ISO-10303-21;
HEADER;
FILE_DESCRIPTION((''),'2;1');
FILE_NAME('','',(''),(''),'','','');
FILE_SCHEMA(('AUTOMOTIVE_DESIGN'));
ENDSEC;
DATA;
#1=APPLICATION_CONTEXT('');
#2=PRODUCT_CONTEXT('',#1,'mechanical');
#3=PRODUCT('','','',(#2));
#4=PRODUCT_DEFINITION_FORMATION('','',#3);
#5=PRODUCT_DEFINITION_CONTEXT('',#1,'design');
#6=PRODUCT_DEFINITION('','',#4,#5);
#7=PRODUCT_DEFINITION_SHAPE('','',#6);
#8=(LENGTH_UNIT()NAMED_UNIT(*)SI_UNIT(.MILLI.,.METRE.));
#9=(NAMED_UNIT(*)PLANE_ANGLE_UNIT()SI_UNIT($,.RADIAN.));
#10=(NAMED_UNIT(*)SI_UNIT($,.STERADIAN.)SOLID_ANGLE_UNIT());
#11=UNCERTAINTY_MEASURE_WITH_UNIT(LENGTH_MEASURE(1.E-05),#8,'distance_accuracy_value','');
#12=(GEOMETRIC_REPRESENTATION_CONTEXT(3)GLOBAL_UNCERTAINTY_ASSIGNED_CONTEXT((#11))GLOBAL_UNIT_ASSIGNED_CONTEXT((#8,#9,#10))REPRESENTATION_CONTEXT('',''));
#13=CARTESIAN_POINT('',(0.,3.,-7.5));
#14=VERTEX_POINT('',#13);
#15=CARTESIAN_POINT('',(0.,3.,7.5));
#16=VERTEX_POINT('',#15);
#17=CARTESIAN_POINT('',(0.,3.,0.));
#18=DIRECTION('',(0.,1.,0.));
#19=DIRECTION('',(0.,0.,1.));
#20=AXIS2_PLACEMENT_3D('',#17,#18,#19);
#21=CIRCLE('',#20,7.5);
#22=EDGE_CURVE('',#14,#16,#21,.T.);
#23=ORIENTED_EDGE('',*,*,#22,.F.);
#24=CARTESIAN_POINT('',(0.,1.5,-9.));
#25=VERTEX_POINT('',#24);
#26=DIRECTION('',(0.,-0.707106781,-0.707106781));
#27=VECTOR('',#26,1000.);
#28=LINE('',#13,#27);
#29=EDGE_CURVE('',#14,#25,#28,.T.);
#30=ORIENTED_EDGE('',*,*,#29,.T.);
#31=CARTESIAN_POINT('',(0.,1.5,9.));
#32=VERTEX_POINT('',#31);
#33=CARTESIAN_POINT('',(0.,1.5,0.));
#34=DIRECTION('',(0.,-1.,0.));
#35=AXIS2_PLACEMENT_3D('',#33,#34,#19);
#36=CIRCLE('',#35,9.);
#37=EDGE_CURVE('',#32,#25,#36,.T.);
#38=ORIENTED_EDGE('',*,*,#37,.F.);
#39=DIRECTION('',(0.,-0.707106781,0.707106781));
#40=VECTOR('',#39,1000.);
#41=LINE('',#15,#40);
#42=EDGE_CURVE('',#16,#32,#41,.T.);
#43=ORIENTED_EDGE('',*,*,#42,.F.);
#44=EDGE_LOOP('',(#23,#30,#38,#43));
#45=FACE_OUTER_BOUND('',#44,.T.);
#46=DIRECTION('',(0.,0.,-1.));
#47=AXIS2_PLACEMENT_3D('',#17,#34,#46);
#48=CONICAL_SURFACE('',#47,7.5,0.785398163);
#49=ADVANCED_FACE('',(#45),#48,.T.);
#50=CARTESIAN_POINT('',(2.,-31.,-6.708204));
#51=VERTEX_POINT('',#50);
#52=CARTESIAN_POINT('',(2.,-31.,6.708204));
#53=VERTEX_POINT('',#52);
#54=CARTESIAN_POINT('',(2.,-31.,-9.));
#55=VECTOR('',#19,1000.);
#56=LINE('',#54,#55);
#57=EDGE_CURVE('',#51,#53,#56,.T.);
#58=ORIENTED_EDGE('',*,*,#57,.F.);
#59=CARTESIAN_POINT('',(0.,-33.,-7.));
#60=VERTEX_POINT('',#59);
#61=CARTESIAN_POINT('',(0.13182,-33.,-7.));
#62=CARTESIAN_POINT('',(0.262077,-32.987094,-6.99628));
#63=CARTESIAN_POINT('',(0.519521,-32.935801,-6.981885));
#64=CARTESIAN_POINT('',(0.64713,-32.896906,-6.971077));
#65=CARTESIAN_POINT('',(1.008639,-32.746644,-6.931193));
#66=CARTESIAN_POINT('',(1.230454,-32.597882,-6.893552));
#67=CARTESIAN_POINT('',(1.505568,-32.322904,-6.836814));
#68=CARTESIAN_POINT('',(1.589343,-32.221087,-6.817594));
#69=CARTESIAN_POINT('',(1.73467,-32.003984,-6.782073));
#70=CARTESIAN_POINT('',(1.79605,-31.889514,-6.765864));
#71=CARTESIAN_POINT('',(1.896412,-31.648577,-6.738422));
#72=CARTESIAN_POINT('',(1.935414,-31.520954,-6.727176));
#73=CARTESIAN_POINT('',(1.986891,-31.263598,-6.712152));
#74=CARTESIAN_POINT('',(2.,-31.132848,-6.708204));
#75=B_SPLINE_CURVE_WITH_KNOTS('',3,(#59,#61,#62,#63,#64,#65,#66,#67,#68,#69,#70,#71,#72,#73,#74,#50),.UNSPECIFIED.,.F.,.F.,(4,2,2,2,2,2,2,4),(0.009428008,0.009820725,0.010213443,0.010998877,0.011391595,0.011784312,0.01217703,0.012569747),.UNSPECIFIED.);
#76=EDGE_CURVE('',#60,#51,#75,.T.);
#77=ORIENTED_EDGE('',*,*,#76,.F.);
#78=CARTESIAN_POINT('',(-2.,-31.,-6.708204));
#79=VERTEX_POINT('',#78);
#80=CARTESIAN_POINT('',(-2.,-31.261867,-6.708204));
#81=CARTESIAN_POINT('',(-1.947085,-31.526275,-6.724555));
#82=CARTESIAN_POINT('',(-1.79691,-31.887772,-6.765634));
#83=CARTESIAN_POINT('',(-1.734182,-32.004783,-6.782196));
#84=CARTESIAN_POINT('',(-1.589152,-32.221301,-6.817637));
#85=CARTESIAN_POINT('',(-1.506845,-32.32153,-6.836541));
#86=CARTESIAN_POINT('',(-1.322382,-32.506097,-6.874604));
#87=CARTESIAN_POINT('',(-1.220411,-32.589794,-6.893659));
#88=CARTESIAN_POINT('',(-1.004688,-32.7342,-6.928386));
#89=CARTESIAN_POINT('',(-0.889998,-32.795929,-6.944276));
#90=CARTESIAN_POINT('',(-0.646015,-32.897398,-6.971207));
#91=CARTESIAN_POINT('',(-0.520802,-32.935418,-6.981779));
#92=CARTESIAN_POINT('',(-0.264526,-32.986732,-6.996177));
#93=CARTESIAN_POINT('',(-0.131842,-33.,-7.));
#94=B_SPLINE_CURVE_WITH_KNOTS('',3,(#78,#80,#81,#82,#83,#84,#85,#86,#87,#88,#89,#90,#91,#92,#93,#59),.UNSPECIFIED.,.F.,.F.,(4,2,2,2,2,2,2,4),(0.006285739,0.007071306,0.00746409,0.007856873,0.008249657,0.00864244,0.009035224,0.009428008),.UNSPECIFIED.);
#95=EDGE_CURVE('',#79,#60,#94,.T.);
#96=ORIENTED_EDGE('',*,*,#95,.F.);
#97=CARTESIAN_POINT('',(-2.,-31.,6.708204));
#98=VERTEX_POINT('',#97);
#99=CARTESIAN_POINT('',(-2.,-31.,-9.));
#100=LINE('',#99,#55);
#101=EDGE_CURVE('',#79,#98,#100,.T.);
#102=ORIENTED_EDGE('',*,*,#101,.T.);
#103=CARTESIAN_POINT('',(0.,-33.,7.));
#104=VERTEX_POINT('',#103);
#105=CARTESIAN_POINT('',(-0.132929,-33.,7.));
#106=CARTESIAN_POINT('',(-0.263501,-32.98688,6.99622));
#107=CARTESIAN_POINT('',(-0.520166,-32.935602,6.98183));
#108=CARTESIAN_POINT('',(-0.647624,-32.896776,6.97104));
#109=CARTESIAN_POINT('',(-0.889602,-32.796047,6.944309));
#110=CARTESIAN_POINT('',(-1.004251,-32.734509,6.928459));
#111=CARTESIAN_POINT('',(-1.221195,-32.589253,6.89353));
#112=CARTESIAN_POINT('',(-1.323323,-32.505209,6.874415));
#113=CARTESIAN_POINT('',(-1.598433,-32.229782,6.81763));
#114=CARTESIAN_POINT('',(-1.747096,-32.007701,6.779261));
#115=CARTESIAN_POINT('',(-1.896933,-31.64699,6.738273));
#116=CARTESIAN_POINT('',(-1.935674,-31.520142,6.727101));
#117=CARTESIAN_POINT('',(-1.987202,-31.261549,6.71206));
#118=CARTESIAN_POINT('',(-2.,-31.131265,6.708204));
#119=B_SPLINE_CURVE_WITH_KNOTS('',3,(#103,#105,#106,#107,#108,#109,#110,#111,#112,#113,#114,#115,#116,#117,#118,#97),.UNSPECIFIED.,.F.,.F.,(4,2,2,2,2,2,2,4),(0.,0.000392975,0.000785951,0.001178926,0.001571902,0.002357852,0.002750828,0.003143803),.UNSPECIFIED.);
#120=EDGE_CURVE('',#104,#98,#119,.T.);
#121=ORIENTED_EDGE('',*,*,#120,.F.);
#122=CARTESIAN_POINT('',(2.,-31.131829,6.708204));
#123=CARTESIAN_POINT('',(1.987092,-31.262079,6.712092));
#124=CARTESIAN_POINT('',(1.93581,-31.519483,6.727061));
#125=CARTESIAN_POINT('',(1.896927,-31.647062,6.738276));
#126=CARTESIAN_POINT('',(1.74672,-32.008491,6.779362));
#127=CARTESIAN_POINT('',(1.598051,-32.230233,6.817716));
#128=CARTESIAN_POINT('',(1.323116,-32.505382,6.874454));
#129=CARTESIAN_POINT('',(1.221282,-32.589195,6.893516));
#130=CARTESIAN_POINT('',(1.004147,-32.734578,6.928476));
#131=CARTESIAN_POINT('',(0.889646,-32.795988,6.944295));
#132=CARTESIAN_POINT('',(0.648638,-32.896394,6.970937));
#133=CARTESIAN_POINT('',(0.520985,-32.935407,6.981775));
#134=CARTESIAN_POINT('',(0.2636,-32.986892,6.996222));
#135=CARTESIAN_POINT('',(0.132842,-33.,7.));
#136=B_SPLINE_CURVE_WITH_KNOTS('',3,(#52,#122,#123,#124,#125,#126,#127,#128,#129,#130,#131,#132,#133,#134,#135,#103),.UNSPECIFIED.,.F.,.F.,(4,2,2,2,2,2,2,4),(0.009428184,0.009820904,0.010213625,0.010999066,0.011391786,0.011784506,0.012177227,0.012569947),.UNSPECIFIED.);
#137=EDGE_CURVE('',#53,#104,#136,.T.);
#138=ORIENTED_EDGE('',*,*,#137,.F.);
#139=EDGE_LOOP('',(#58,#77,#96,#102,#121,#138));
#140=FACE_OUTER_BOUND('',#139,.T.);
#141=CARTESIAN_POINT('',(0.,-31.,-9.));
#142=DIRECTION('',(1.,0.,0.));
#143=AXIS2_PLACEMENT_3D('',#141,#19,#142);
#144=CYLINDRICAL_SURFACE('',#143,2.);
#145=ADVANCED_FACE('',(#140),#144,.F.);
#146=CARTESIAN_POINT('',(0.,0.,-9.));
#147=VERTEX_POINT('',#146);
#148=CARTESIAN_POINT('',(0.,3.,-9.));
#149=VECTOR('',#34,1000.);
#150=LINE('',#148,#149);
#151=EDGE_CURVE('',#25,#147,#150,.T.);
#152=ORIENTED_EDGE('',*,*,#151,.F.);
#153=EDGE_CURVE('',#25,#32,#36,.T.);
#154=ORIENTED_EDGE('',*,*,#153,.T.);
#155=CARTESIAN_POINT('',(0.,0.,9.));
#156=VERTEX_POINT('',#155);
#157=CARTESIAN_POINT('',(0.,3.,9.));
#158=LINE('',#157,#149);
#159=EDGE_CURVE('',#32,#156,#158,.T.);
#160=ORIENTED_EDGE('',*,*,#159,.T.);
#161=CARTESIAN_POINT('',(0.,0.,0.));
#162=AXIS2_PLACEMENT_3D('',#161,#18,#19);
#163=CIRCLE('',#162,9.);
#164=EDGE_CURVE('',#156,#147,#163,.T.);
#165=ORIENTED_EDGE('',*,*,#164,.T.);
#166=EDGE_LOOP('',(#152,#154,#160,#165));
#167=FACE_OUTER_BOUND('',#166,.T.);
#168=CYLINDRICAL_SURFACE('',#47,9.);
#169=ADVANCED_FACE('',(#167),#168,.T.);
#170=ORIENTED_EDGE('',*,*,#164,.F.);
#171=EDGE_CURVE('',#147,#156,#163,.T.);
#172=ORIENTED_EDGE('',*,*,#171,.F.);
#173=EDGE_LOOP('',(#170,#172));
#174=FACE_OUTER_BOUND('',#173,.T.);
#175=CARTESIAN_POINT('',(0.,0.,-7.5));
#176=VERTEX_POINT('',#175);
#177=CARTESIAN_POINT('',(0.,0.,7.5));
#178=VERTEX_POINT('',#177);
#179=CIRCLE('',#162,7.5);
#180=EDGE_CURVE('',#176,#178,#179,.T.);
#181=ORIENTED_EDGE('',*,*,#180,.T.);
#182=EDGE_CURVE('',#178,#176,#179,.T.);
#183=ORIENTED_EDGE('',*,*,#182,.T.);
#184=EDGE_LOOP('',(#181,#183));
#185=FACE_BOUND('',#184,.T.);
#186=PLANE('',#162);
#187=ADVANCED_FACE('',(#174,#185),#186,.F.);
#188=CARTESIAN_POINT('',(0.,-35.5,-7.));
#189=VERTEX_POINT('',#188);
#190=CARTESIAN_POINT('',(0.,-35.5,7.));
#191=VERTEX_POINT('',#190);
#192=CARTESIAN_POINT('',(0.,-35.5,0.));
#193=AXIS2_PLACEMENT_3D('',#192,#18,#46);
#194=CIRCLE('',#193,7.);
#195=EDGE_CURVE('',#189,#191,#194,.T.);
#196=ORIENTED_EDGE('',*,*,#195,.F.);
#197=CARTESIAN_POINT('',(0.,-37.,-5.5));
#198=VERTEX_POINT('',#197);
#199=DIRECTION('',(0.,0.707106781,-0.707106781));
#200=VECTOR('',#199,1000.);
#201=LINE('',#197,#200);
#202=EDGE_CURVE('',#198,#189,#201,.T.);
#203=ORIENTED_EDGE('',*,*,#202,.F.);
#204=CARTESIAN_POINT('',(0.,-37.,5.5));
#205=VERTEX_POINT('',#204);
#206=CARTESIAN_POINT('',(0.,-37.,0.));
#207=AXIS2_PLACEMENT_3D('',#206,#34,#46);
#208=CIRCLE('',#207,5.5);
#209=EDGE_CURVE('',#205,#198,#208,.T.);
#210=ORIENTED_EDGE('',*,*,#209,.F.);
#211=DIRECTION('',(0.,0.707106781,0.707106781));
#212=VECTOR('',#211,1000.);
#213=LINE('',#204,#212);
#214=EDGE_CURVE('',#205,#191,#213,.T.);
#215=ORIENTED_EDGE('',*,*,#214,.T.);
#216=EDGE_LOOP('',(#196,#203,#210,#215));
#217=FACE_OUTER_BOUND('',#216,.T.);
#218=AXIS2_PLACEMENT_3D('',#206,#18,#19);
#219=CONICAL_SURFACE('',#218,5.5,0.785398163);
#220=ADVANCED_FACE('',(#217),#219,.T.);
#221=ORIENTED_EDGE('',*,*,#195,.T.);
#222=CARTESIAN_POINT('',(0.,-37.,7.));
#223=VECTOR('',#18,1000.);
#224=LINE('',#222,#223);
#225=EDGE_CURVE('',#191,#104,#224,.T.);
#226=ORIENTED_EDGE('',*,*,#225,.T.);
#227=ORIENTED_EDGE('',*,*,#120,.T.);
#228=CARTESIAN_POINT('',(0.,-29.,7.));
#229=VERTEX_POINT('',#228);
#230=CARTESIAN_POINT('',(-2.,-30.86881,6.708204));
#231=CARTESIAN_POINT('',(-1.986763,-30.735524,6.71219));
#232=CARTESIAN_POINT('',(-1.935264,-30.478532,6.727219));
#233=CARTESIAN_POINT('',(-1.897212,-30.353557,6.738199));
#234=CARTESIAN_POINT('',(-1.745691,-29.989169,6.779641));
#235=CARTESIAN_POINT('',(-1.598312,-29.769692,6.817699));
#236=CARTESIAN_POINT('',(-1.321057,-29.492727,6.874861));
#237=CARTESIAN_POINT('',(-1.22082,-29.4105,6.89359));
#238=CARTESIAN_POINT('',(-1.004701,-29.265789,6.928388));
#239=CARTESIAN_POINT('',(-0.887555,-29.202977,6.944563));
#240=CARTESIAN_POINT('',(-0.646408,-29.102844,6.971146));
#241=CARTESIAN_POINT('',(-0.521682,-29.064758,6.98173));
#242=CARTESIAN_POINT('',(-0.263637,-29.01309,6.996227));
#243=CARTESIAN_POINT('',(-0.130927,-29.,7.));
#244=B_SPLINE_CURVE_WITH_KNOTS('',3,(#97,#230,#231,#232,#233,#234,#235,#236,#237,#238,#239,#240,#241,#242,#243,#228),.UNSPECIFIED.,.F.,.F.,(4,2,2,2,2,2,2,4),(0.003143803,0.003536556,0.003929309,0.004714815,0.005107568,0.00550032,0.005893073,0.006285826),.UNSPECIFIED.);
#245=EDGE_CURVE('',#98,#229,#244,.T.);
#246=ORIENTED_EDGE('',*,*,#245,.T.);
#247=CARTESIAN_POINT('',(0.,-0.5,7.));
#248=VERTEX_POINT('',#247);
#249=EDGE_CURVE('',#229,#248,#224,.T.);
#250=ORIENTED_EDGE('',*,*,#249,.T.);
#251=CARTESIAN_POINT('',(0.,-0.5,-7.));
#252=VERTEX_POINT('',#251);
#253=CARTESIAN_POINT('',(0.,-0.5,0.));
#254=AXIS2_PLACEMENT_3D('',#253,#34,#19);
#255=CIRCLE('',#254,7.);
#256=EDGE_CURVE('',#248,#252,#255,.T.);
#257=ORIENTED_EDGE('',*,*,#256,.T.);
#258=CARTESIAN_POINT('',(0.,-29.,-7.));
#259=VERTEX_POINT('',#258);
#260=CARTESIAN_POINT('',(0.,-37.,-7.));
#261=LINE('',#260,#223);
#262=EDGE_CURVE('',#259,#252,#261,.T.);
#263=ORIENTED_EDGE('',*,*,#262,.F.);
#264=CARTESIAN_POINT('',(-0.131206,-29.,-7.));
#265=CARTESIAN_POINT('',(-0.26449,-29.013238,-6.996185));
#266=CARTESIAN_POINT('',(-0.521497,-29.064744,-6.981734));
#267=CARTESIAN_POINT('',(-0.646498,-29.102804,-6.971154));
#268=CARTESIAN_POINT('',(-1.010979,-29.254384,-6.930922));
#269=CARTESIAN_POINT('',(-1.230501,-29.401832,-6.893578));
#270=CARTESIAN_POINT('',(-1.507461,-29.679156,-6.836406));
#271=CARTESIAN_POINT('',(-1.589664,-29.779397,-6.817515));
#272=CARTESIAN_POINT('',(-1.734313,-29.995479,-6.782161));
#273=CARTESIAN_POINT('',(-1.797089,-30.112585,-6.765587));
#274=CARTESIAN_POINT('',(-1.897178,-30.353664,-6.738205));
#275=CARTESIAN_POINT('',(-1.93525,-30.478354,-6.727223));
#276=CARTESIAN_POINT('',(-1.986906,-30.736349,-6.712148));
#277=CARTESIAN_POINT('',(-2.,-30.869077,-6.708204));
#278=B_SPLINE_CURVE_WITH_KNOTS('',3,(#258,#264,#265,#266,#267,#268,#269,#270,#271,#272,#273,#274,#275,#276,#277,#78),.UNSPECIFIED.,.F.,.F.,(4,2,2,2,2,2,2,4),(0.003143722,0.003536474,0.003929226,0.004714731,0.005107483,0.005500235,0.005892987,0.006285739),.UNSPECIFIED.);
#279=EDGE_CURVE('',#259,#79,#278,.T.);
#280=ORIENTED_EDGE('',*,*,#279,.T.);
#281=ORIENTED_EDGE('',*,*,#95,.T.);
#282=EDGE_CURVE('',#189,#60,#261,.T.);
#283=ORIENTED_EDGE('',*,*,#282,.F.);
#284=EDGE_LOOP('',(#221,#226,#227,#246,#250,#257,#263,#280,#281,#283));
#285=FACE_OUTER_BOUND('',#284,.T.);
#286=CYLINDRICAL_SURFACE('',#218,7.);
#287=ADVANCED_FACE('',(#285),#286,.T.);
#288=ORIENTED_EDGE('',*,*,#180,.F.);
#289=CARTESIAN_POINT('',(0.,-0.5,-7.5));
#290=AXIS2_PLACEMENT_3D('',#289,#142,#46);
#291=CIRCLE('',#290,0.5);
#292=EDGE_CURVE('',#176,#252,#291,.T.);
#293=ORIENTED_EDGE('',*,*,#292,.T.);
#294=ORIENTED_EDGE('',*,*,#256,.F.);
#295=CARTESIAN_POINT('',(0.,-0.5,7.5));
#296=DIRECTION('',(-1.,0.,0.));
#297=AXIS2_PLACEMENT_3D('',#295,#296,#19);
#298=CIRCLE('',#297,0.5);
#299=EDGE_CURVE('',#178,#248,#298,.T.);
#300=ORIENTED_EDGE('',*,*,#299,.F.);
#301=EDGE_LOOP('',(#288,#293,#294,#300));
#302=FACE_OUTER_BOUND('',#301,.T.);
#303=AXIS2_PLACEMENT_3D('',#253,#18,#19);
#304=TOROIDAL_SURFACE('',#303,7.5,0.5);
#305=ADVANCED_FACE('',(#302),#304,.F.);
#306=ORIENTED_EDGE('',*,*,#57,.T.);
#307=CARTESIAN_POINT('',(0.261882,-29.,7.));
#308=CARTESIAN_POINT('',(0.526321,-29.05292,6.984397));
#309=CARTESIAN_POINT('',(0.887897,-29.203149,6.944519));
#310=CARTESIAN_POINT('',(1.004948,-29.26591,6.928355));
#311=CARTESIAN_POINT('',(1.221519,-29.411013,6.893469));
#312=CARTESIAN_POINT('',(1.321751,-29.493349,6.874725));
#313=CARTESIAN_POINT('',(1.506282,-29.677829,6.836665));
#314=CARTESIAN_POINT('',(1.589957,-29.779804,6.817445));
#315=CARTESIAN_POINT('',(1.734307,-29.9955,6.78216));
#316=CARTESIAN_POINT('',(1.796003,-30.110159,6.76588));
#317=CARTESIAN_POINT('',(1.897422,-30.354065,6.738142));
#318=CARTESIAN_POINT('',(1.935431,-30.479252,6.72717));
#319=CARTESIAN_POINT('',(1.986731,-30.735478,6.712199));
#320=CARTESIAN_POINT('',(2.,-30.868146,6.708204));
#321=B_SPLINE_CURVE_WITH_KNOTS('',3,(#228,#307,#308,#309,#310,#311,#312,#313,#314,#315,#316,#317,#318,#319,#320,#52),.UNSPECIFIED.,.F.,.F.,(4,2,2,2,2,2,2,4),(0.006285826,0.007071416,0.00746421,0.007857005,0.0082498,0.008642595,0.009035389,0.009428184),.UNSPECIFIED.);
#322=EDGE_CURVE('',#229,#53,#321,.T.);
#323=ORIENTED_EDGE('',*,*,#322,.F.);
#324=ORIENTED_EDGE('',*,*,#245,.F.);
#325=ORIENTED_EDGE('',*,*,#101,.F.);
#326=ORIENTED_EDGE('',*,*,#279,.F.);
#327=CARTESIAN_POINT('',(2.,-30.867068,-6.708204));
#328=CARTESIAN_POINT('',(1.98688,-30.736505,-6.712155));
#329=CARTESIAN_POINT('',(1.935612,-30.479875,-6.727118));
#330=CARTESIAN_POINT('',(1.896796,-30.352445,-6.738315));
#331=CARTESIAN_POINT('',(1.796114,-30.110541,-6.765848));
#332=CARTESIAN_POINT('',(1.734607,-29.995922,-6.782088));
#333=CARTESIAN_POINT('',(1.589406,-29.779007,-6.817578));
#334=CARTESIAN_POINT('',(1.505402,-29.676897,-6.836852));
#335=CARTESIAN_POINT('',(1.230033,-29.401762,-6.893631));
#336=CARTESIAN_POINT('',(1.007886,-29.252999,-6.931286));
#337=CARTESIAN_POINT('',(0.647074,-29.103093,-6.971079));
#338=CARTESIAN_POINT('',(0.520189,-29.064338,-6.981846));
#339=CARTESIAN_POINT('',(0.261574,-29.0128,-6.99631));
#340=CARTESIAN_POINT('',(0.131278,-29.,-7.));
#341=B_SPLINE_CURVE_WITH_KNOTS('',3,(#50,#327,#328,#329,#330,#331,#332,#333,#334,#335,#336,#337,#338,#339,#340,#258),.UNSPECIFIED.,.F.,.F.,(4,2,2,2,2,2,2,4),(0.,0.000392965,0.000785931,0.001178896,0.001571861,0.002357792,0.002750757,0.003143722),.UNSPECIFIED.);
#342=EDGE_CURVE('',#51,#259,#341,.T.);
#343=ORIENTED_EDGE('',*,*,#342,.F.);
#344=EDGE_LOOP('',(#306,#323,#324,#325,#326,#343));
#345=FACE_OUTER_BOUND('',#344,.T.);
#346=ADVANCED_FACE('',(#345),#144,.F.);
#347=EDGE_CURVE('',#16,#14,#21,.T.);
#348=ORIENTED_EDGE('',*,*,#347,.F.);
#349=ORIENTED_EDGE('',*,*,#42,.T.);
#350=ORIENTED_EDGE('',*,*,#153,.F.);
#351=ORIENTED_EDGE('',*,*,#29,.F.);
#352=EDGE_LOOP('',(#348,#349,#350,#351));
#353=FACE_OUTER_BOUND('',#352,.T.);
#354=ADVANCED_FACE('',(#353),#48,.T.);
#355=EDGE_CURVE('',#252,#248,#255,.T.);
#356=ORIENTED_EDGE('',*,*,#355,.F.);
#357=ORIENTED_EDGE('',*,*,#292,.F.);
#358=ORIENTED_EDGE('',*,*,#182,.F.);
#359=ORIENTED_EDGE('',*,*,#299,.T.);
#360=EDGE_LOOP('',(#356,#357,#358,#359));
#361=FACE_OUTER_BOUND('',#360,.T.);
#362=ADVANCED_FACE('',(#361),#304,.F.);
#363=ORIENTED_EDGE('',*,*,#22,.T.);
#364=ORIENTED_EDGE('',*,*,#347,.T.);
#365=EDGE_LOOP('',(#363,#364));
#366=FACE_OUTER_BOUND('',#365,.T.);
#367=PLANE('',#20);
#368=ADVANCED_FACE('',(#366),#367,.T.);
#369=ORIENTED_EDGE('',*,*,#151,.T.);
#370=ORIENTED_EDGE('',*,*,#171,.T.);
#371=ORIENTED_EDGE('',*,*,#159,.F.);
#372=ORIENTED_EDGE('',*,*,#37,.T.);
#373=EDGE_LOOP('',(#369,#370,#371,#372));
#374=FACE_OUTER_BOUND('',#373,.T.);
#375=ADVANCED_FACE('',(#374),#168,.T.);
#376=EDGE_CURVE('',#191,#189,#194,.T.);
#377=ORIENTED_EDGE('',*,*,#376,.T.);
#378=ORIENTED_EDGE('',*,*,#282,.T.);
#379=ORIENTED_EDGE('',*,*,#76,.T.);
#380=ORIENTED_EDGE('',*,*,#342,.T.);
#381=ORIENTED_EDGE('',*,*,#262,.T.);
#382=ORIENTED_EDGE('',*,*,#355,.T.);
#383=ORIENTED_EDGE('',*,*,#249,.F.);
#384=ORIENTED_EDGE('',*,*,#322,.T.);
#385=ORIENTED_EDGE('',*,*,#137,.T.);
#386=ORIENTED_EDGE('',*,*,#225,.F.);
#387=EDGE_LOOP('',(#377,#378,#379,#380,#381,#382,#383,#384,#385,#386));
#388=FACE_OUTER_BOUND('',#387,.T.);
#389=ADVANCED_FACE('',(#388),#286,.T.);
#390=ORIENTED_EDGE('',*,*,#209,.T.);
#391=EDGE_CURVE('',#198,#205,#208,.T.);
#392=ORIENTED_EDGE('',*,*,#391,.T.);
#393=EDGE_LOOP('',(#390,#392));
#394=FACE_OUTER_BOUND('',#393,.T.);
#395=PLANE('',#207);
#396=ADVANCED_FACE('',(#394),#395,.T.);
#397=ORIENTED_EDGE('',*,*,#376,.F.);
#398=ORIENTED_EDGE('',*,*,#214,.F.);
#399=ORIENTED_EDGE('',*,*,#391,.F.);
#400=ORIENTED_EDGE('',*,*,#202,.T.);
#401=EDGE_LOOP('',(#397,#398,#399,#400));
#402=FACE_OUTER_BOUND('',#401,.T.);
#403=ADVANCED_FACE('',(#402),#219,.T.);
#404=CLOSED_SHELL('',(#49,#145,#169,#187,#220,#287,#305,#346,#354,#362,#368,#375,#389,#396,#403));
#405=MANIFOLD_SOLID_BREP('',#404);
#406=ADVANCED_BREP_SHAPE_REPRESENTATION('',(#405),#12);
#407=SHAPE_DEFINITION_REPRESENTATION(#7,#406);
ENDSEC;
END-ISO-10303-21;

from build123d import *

# Parameters (mm, degrees)
SKETCH_1_R               = 9
EXTRUDE_1_DEPTH          = 3
SKETCH_2_R               = 7
EXTRUDE_2_DEPTH          = 37
CHAMFER_1_SIZE           = 1.5
CUT_EXTRUDE_2_DEPTH      = 40.127995093
CUT_EXTRUDE_2_DEPTH_BACK = 40.127995093
SKETCH_10_R              = 2
FILLET_1_R               = 0.5


with BuildPart() as part:
    # 草图1 → 凸台-拉伸1 (new body)
    with BuildSketch(Plane(origin=(0, 0, 0), x_dir=(1, 0, 0), z_dir=(0, 1, 0))):
        with Locations(Location((0, 0, 0), (0, 0, 270))):
            Circle(SKETCH_1_R)
    extrude(amount=EXTRUDE_1_DEPTH)

    # 草图2 → 凸台-拉伸2 (add)
    with BuildSketch(Plane.XZ):
        with Locations(Location((0, 0, 0), (0, 0, 270))):
            Circle(SKETCH_2_R)
    extrude(amount=EXTRUDE_2_DEPTH)

    # 倒角1
    chamfer_1_edges = [part.edges().sort_by_distance(p)[0] for p in [
        (0, 3, -9),
        (0, -37, 7),
    ]]
    chamfer(chamfer_1_edges, length=CHAMFER_1_SIZE)

    # 草图10 → 切除-拉伸2 (cut, two sides: drawn at the far end of the back side and taken through both)
    with BuildSketch(Plane.XY.offset(-CUT_EXTRUDE_2_DEPTH_BACK)):
        with Locations(Location((0, -31, 0), (0, 0, 270.00000003))):
            Circle(SKETCH_10_R)
    extrude(amount=CUT_EXTRUDE_2_DEPTH + CUT_EXTRUDE_2_DEPTH_BACK, mode=Mode.SUBTRACT)

    # 圆角1
    fillet_1_edges = [part.edges().sort_by_distance(p)[0] for p in [
        (0, 0, 7),
    ]]
    fillet(fillet_1_edges, radius=FILLET_1_R)


solid = part.part
